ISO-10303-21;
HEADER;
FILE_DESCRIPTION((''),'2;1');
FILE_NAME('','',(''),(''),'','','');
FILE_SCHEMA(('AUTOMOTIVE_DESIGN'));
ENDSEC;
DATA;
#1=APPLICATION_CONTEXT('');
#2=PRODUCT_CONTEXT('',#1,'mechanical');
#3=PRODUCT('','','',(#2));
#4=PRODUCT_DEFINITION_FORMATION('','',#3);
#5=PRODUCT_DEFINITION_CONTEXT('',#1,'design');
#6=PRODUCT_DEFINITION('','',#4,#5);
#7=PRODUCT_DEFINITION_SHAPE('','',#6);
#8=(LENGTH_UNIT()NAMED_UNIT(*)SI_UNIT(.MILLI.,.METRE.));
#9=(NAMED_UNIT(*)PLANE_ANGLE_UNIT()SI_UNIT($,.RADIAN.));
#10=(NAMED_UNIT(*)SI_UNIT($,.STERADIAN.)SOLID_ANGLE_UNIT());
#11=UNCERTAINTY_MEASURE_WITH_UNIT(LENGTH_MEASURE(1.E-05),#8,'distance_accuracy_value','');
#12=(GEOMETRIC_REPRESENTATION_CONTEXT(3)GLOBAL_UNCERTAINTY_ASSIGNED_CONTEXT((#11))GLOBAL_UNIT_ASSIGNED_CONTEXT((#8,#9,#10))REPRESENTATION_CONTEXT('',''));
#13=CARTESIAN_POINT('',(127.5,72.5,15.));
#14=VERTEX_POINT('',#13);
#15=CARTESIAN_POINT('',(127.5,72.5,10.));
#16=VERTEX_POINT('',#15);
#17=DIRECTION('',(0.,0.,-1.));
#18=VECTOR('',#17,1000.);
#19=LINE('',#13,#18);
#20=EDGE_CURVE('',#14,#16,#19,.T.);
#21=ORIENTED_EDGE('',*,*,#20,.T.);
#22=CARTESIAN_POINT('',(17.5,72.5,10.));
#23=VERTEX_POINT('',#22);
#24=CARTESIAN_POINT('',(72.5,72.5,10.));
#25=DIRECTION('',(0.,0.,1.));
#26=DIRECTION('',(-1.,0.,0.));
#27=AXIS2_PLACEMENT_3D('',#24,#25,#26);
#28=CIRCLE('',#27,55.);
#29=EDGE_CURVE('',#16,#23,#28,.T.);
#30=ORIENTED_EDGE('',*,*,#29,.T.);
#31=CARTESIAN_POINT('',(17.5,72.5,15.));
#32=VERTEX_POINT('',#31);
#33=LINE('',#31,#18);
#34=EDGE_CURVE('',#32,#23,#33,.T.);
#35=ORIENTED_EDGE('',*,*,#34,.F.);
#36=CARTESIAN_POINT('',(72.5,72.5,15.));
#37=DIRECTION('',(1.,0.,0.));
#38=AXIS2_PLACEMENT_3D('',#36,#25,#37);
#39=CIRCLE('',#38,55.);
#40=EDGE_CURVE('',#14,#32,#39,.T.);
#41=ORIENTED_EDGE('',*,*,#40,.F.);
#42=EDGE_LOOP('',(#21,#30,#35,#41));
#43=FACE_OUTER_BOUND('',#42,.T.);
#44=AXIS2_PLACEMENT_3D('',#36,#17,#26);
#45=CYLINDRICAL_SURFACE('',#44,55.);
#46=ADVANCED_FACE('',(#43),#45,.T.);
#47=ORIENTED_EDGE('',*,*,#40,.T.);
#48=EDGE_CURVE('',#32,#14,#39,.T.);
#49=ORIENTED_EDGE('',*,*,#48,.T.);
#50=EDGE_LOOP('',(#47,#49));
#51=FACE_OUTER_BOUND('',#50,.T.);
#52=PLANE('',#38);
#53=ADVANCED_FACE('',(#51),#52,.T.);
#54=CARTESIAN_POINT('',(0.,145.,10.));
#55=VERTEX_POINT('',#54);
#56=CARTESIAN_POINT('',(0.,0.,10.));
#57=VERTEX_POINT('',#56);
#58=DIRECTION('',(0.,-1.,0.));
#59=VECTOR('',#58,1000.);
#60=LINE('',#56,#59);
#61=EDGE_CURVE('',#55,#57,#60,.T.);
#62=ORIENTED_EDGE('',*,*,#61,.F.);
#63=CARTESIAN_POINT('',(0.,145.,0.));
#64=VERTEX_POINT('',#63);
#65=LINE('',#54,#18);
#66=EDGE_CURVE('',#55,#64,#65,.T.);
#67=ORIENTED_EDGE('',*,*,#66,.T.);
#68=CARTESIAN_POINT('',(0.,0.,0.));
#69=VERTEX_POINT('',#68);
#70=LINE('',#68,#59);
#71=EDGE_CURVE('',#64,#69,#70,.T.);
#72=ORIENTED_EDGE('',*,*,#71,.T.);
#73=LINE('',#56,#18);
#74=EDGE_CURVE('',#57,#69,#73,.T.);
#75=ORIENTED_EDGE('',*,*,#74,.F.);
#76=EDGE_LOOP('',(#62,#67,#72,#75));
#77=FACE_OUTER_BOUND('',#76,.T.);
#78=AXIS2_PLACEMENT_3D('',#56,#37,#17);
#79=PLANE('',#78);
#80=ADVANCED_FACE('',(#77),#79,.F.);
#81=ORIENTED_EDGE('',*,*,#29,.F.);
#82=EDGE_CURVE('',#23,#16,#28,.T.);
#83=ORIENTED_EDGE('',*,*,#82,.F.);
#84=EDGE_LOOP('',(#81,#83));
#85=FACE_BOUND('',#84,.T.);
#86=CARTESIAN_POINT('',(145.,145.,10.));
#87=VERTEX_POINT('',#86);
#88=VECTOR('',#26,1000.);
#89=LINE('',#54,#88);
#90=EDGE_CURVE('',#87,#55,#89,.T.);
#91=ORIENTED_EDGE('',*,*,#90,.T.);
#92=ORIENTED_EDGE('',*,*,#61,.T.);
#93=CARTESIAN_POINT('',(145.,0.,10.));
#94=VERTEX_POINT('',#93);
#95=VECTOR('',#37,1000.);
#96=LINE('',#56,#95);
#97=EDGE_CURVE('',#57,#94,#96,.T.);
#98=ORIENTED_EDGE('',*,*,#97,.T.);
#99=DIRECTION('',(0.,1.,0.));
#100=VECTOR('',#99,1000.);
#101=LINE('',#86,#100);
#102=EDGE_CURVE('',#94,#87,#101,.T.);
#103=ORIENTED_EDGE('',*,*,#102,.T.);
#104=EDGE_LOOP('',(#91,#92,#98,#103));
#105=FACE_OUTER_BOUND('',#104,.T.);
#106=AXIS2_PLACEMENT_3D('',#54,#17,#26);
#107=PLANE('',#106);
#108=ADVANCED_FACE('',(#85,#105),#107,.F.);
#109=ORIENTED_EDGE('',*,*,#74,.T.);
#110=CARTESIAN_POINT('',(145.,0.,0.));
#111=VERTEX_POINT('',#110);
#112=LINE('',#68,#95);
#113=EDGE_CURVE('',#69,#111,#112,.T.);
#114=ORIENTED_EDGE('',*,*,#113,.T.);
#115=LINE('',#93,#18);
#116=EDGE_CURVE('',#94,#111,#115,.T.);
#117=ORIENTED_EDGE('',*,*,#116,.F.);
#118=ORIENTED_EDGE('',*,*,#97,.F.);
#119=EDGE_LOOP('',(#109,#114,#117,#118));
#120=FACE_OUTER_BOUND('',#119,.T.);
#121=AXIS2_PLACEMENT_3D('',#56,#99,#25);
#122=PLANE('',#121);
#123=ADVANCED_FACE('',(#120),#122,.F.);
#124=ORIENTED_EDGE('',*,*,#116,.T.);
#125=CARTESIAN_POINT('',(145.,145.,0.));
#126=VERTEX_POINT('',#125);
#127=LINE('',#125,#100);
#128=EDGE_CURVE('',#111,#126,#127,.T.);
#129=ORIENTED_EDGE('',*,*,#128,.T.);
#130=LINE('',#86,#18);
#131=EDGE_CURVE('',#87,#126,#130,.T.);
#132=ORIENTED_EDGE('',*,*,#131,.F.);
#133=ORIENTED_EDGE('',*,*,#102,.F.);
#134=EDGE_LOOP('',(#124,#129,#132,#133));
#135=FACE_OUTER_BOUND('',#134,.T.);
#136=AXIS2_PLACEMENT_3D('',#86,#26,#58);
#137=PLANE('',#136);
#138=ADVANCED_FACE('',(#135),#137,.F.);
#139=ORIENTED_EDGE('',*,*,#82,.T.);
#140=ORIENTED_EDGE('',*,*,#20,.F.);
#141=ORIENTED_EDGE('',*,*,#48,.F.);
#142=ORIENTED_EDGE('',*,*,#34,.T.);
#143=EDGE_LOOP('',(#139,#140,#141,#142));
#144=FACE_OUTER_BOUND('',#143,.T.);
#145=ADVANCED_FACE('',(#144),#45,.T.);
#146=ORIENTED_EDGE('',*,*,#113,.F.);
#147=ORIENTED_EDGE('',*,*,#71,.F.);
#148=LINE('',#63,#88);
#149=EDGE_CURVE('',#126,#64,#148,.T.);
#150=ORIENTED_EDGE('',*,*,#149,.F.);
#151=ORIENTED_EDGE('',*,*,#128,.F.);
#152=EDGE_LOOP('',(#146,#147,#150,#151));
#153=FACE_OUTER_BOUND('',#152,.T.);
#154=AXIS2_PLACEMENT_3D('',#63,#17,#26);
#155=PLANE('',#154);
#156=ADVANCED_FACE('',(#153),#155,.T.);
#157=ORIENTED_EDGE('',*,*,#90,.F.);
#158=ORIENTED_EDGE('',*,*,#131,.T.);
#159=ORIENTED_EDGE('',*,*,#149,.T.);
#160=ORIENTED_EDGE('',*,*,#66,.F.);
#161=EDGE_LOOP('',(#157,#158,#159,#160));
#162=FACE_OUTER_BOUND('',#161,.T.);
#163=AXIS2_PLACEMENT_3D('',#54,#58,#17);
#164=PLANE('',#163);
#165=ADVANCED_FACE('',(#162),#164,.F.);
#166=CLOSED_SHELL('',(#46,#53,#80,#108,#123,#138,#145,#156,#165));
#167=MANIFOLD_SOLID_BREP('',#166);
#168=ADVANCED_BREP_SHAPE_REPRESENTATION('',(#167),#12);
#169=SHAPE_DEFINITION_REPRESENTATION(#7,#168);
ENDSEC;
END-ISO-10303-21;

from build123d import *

# Parameters (mm, degrees)
SKETCH1_W           = 145
SKETCH1_H           = 145
BOSS_EXTRUDE1_DEPTH = 10
SKETCH2_R           = 55
BOSS_EXTRUDE2_DEPTH = 5


with BuildPart() as part:
    # Sketch1 → Boss-Extrude1 (new body)
    with BuildSketch(Plane.XY):
        with Locations((72.5, 72.5)):
            Rectangle(SKETCH1_W, SKETCH1_H)
    extrude(amount=BOSS_EXTRUDE1_DEPTH)

    # Sketch2 → Boss-Extrude2 (add)
    with BuildSketch(Plane.XY.offset(10)):
        with Locations(Location((72.5, 72.5, 0), (0, 0, 180))):
            Circle(SKETCH2_R)
    extrude(amount=BOSS_EXTRUDE2_DEPTH)


solid = part.part
